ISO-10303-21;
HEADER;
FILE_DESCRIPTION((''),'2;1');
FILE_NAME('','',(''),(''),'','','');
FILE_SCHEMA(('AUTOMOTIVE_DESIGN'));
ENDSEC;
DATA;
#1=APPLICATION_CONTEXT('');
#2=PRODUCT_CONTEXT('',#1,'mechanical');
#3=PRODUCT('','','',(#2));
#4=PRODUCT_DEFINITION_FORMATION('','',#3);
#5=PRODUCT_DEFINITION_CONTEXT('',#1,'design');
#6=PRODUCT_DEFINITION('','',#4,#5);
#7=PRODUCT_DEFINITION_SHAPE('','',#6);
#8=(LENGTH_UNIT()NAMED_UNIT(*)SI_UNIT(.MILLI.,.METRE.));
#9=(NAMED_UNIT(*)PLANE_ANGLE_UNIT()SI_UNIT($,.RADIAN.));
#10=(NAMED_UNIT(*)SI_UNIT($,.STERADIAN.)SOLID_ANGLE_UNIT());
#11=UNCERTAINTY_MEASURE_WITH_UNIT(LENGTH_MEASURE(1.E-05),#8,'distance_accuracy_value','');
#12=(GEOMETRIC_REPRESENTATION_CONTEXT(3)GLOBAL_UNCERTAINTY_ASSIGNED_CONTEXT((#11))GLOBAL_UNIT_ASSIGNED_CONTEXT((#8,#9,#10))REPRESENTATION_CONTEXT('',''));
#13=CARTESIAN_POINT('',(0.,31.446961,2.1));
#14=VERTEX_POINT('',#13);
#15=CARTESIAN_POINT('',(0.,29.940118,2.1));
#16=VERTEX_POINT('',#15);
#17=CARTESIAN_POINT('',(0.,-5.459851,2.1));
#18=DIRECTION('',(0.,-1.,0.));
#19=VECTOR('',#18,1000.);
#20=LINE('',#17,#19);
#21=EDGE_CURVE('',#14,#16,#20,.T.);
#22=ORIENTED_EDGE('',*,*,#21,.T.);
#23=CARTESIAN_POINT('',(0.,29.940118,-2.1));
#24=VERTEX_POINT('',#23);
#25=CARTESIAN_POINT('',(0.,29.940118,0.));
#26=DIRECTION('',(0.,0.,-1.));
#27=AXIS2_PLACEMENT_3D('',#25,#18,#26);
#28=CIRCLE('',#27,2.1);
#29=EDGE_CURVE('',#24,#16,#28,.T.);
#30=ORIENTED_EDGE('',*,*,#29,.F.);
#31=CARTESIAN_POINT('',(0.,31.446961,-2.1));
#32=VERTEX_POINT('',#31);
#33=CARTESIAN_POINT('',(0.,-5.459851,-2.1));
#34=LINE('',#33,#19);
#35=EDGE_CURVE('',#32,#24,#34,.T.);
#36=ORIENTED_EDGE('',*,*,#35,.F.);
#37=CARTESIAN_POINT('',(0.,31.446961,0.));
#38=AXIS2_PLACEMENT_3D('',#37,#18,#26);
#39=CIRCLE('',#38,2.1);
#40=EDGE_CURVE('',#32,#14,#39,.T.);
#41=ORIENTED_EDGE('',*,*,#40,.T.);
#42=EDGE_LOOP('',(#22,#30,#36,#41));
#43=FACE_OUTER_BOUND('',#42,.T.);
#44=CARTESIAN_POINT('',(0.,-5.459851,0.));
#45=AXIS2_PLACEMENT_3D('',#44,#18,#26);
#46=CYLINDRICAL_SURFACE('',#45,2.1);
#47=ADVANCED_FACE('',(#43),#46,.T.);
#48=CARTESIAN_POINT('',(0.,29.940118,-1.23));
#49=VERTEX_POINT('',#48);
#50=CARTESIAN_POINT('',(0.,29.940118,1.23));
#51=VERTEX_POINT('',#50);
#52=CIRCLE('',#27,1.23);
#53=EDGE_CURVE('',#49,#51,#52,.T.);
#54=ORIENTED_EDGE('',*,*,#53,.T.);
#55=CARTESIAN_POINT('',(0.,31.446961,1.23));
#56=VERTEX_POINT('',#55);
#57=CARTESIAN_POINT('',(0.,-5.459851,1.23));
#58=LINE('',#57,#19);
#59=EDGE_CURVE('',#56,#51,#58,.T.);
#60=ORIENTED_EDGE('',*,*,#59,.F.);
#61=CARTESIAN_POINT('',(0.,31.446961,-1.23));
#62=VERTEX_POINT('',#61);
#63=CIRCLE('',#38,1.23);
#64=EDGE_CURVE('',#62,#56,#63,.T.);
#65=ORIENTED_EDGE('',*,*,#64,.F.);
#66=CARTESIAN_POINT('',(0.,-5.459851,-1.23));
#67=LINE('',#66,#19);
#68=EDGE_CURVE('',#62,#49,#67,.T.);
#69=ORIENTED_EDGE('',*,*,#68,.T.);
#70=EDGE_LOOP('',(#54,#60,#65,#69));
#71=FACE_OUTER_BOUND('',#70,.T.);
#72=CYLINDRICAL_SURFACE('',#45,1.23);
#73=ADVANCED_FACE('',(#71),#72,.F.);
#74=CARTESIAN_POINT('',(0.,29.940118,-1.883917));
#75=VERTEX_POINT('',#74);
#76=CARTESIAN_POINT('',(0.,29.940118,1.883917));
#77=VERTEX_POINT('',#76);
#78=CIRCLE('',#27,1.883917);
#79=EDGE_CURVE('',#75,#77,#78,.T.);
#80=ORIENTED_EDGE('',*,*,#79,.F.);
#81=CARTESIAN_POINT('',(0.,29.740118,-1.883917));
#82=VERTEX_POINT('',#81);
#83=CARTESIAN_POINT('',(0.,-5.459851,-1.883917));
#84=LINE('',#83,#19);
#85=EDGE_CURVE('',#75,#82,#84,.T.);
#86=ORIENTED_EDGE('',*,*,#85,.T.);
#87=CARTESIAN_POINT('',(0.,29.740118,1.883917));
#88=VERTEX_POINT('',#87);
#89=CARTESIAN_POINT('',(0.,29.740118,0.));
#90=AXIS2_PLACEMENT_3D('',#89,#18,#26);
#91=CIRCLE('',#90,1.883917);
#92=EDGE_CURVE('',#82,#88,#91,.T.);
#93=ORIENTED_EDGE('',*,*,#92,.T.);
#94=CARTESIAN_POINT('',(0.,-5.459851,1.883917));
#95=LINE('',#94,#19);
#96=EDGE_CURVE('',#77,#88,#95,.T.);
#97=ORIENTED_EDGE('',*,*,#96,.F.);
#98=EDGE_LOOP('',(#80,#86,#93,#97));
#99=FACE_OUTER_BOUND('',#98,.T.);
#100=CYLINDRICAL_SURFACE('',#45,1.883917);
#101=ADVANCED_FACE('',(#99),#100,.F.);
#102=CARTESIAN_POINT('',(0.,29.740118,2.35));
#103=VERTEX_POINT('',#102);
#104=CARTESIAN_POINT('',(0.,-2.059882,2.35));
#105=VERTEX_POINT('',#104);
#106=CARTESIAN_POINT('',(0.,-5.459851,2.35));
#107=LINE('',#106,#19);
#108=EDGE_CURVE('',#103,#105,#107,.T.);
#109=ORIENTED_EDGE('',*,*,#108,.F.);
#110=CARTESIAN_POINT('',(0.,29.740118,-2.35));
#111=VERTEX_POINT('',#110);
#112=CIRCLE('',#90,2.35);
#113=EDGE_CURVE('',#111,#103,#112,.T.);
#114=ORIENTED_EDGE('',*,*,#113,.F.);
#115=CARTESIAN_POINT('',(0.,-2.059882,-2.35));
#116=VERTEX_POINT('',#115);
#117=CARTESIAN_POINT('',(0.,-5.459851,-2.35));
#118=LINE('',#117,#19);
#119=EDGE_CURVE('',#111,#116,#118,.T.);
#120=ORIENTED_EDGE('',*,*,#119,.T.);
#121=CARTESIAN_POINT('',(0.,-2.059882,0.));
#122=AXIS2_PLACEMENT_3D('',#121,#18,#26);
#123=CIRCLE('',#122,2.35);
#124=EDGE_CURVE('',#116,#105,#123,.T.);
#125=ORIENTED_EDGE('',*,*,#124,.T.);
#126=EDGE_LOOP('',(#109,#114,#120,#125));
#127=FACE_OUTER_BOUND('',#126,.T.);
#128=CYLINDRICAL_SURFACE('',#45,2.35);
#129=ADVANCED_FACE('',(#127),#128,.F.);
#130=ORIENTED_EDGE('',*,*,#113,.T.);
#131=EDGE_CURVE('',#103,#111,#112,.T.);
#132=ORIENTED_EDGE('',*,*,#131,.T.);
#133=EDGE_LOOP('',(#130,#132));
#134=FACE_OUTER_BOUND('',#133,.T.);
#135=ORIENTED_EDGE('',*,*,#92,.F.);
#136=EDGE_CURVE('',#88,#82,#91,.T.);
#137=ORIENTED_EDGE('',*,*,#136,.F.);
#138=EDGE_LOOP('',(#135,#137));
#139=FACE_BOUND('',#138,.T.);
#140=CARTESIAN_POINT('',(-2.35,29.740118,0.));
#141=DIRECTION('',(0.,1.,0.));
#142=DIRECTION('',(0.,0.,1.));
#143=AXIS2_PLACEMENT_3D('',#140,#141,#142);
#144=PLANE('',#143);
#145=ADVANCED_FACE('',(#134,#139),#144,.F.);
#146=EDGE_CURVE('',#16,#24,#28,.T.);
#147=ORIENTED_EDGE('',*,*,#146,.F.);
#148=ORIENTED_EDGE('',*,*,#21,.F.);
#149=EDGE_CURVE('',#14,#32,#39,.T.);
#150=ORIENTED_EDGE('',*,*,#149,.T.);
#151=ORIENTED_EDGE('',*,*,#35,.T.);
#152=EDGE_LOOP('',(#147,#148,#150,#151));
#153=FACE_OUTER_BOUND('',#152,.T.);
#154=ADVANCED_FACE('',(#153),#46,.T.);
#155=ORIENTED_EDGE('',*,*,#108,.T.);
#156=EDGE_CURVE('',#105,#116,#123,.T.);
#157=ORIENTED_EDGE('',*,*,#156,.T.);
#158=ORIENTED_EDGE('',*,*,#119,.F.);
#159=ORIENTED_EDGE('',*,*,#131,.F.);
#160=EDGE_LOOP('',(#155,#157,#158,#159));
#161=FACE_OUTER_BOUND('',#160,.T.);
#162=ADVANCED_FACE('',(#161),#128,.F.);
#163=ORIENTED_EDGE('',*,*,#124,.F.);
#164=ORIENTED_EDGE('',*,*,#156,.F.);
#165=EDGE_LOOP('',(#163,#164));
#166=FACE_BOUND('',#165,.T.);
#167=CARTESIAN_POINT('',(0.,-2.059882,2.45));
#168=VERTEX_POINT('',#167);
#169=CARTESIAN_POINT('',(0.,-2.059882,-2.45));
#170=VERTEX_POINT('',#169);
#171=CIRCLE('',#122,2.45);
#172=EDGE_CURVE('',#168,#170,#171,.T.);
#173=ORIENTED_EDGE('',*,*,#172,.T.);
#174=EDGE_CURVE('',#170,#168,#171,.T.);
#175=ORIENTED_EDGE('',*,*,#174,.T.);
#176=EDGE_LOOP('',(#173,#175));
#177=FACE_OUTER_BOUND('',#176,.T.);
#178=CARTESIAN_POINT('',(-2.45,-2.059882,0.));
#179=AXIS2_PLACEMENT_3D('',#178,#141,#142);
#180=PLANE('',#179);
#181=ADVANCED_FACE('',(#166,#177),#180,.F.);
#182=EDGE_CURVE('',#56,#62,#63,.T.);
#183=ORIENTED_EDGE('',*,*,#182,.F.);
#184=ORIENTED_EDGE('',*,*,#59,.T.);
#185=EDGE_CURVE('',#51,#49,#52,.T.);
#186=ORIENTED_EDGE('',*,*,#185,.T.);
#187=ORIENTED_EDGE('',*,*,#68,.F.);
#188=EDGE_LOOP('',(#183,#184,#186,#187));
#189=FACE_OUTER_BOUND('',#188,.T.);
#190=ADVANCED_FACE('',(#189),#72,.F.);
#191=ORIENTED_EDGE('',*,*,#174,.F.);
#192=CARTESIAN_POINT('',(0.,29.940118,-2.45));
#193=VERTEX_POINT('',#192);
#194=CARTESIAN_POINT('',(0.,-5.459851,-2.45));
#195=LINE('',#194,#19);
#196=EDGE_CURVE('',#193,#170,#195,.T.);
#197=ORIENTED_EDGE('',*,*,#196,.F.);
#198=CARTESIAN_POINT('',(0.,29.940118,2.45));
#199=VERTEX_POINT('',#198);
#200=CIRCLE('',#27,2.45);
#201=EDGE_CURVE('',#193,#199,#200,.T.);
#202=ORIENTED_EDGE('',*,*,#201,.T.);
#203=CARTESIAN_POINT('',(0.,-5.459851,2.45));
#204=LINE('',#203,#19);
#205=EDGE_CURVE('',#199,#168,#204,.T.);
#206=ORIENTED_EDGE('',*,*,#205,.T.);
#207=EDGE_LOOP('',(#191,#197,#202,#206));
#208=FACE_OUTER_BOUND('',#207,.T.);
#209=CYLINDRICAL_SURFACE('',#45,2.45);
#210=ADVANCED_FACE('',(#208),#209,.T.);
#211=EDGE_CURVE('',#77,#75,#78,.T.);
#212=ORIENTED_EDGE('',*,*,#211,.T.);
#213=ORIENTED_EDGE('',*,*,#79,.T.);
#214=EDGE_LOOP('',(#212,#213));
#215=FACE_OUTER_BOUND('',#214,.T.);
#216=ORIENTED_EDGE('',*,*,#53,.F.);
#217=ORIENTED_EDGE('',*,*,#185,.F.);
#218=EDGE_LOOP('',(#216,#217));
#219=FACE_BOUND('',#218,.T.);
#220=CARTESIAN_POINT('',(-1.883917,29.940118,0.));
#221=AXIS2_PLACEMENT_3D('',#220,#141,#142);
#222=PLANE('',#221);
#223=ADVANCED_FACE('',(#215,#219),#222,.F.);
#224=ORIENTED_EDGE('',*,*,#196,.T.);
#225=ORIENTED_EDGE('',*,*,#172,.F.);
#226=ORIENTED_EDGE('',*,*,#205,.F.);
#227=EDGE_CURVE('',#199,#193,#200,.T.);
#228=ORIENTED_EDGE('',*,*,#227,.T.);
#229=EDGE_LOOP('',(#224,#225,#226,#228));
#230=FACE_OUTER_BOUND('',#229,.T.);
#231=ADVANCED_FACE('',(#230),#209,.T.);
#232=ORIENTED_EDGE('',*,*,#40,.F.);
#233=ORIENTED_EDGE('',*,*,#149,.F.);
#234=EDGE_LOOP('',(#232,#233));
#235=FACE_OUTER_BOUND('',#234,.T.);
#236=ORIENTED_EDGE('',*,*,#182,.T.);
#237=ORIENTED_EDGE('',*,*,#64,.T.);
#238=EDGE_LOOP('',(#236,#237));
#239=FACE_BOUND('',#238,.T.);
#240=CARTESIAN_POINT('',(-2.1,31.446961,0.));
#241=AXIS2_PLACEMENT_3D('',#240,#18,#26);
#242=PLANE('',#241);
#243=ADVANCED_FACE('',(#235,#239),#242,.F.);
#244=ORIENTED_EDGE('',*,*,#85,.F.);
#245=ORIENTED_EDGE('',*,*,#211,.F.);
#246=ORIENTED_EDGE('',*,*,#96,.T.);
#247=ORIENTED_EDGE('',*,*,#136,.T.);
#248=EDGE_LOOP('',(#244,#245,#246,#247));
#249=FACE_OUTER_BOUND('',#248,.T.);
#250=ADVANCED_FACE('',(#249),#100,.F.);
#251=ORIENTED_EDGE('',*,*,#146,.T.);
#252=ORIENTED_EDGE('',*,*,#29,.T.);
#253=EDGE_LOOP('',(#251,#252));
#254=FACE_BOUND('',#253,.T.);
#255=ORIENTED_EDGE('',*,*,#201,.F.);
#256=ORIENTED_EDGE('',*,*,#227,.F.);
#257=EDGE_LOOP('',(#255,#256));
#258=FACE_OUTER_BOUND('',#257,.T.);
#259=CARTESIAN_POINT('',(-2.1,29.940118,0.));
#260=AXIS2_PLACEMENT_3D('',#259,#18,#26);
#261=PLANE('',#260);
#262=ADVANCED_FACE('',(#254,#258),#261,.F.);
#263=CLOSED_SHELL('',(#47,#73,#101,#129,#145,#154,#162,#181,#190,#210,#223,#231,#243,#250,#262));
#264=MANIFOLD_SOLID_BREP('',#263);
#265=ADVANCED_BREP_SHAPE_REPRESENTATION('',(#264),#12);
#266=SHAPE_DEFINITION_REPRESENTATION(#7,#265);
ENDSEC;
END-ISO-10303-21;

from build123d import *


with BuildPart() as part:
    # Sketch1 → Revolve1 (revolve)
    with BuildSketch(Plane.XY, mode=Mode.PRIVATE) as revolve1_sk:
        Polygon((-2.45, 29.940117832), (-2.45, -2.059882168), (-2.35, -2.059882168), (-2.35, 29.740117832), (-1.883917375, 29.740117832), (-1.883917375, 29.940117832), (-1.23, 29.940117832), (-1.23, 31.44696074), (-2.1, 31.44696074), (-2.1, 29.940117832), align=None)
    revolve(revolve1_sk.sketch.rotate(Axis((0, -5.459851486, 0), (0, 1, 0)), 270), axis=Axis((0, -5.459851486, 0), (0, 1, 0)))


solid = part.part
